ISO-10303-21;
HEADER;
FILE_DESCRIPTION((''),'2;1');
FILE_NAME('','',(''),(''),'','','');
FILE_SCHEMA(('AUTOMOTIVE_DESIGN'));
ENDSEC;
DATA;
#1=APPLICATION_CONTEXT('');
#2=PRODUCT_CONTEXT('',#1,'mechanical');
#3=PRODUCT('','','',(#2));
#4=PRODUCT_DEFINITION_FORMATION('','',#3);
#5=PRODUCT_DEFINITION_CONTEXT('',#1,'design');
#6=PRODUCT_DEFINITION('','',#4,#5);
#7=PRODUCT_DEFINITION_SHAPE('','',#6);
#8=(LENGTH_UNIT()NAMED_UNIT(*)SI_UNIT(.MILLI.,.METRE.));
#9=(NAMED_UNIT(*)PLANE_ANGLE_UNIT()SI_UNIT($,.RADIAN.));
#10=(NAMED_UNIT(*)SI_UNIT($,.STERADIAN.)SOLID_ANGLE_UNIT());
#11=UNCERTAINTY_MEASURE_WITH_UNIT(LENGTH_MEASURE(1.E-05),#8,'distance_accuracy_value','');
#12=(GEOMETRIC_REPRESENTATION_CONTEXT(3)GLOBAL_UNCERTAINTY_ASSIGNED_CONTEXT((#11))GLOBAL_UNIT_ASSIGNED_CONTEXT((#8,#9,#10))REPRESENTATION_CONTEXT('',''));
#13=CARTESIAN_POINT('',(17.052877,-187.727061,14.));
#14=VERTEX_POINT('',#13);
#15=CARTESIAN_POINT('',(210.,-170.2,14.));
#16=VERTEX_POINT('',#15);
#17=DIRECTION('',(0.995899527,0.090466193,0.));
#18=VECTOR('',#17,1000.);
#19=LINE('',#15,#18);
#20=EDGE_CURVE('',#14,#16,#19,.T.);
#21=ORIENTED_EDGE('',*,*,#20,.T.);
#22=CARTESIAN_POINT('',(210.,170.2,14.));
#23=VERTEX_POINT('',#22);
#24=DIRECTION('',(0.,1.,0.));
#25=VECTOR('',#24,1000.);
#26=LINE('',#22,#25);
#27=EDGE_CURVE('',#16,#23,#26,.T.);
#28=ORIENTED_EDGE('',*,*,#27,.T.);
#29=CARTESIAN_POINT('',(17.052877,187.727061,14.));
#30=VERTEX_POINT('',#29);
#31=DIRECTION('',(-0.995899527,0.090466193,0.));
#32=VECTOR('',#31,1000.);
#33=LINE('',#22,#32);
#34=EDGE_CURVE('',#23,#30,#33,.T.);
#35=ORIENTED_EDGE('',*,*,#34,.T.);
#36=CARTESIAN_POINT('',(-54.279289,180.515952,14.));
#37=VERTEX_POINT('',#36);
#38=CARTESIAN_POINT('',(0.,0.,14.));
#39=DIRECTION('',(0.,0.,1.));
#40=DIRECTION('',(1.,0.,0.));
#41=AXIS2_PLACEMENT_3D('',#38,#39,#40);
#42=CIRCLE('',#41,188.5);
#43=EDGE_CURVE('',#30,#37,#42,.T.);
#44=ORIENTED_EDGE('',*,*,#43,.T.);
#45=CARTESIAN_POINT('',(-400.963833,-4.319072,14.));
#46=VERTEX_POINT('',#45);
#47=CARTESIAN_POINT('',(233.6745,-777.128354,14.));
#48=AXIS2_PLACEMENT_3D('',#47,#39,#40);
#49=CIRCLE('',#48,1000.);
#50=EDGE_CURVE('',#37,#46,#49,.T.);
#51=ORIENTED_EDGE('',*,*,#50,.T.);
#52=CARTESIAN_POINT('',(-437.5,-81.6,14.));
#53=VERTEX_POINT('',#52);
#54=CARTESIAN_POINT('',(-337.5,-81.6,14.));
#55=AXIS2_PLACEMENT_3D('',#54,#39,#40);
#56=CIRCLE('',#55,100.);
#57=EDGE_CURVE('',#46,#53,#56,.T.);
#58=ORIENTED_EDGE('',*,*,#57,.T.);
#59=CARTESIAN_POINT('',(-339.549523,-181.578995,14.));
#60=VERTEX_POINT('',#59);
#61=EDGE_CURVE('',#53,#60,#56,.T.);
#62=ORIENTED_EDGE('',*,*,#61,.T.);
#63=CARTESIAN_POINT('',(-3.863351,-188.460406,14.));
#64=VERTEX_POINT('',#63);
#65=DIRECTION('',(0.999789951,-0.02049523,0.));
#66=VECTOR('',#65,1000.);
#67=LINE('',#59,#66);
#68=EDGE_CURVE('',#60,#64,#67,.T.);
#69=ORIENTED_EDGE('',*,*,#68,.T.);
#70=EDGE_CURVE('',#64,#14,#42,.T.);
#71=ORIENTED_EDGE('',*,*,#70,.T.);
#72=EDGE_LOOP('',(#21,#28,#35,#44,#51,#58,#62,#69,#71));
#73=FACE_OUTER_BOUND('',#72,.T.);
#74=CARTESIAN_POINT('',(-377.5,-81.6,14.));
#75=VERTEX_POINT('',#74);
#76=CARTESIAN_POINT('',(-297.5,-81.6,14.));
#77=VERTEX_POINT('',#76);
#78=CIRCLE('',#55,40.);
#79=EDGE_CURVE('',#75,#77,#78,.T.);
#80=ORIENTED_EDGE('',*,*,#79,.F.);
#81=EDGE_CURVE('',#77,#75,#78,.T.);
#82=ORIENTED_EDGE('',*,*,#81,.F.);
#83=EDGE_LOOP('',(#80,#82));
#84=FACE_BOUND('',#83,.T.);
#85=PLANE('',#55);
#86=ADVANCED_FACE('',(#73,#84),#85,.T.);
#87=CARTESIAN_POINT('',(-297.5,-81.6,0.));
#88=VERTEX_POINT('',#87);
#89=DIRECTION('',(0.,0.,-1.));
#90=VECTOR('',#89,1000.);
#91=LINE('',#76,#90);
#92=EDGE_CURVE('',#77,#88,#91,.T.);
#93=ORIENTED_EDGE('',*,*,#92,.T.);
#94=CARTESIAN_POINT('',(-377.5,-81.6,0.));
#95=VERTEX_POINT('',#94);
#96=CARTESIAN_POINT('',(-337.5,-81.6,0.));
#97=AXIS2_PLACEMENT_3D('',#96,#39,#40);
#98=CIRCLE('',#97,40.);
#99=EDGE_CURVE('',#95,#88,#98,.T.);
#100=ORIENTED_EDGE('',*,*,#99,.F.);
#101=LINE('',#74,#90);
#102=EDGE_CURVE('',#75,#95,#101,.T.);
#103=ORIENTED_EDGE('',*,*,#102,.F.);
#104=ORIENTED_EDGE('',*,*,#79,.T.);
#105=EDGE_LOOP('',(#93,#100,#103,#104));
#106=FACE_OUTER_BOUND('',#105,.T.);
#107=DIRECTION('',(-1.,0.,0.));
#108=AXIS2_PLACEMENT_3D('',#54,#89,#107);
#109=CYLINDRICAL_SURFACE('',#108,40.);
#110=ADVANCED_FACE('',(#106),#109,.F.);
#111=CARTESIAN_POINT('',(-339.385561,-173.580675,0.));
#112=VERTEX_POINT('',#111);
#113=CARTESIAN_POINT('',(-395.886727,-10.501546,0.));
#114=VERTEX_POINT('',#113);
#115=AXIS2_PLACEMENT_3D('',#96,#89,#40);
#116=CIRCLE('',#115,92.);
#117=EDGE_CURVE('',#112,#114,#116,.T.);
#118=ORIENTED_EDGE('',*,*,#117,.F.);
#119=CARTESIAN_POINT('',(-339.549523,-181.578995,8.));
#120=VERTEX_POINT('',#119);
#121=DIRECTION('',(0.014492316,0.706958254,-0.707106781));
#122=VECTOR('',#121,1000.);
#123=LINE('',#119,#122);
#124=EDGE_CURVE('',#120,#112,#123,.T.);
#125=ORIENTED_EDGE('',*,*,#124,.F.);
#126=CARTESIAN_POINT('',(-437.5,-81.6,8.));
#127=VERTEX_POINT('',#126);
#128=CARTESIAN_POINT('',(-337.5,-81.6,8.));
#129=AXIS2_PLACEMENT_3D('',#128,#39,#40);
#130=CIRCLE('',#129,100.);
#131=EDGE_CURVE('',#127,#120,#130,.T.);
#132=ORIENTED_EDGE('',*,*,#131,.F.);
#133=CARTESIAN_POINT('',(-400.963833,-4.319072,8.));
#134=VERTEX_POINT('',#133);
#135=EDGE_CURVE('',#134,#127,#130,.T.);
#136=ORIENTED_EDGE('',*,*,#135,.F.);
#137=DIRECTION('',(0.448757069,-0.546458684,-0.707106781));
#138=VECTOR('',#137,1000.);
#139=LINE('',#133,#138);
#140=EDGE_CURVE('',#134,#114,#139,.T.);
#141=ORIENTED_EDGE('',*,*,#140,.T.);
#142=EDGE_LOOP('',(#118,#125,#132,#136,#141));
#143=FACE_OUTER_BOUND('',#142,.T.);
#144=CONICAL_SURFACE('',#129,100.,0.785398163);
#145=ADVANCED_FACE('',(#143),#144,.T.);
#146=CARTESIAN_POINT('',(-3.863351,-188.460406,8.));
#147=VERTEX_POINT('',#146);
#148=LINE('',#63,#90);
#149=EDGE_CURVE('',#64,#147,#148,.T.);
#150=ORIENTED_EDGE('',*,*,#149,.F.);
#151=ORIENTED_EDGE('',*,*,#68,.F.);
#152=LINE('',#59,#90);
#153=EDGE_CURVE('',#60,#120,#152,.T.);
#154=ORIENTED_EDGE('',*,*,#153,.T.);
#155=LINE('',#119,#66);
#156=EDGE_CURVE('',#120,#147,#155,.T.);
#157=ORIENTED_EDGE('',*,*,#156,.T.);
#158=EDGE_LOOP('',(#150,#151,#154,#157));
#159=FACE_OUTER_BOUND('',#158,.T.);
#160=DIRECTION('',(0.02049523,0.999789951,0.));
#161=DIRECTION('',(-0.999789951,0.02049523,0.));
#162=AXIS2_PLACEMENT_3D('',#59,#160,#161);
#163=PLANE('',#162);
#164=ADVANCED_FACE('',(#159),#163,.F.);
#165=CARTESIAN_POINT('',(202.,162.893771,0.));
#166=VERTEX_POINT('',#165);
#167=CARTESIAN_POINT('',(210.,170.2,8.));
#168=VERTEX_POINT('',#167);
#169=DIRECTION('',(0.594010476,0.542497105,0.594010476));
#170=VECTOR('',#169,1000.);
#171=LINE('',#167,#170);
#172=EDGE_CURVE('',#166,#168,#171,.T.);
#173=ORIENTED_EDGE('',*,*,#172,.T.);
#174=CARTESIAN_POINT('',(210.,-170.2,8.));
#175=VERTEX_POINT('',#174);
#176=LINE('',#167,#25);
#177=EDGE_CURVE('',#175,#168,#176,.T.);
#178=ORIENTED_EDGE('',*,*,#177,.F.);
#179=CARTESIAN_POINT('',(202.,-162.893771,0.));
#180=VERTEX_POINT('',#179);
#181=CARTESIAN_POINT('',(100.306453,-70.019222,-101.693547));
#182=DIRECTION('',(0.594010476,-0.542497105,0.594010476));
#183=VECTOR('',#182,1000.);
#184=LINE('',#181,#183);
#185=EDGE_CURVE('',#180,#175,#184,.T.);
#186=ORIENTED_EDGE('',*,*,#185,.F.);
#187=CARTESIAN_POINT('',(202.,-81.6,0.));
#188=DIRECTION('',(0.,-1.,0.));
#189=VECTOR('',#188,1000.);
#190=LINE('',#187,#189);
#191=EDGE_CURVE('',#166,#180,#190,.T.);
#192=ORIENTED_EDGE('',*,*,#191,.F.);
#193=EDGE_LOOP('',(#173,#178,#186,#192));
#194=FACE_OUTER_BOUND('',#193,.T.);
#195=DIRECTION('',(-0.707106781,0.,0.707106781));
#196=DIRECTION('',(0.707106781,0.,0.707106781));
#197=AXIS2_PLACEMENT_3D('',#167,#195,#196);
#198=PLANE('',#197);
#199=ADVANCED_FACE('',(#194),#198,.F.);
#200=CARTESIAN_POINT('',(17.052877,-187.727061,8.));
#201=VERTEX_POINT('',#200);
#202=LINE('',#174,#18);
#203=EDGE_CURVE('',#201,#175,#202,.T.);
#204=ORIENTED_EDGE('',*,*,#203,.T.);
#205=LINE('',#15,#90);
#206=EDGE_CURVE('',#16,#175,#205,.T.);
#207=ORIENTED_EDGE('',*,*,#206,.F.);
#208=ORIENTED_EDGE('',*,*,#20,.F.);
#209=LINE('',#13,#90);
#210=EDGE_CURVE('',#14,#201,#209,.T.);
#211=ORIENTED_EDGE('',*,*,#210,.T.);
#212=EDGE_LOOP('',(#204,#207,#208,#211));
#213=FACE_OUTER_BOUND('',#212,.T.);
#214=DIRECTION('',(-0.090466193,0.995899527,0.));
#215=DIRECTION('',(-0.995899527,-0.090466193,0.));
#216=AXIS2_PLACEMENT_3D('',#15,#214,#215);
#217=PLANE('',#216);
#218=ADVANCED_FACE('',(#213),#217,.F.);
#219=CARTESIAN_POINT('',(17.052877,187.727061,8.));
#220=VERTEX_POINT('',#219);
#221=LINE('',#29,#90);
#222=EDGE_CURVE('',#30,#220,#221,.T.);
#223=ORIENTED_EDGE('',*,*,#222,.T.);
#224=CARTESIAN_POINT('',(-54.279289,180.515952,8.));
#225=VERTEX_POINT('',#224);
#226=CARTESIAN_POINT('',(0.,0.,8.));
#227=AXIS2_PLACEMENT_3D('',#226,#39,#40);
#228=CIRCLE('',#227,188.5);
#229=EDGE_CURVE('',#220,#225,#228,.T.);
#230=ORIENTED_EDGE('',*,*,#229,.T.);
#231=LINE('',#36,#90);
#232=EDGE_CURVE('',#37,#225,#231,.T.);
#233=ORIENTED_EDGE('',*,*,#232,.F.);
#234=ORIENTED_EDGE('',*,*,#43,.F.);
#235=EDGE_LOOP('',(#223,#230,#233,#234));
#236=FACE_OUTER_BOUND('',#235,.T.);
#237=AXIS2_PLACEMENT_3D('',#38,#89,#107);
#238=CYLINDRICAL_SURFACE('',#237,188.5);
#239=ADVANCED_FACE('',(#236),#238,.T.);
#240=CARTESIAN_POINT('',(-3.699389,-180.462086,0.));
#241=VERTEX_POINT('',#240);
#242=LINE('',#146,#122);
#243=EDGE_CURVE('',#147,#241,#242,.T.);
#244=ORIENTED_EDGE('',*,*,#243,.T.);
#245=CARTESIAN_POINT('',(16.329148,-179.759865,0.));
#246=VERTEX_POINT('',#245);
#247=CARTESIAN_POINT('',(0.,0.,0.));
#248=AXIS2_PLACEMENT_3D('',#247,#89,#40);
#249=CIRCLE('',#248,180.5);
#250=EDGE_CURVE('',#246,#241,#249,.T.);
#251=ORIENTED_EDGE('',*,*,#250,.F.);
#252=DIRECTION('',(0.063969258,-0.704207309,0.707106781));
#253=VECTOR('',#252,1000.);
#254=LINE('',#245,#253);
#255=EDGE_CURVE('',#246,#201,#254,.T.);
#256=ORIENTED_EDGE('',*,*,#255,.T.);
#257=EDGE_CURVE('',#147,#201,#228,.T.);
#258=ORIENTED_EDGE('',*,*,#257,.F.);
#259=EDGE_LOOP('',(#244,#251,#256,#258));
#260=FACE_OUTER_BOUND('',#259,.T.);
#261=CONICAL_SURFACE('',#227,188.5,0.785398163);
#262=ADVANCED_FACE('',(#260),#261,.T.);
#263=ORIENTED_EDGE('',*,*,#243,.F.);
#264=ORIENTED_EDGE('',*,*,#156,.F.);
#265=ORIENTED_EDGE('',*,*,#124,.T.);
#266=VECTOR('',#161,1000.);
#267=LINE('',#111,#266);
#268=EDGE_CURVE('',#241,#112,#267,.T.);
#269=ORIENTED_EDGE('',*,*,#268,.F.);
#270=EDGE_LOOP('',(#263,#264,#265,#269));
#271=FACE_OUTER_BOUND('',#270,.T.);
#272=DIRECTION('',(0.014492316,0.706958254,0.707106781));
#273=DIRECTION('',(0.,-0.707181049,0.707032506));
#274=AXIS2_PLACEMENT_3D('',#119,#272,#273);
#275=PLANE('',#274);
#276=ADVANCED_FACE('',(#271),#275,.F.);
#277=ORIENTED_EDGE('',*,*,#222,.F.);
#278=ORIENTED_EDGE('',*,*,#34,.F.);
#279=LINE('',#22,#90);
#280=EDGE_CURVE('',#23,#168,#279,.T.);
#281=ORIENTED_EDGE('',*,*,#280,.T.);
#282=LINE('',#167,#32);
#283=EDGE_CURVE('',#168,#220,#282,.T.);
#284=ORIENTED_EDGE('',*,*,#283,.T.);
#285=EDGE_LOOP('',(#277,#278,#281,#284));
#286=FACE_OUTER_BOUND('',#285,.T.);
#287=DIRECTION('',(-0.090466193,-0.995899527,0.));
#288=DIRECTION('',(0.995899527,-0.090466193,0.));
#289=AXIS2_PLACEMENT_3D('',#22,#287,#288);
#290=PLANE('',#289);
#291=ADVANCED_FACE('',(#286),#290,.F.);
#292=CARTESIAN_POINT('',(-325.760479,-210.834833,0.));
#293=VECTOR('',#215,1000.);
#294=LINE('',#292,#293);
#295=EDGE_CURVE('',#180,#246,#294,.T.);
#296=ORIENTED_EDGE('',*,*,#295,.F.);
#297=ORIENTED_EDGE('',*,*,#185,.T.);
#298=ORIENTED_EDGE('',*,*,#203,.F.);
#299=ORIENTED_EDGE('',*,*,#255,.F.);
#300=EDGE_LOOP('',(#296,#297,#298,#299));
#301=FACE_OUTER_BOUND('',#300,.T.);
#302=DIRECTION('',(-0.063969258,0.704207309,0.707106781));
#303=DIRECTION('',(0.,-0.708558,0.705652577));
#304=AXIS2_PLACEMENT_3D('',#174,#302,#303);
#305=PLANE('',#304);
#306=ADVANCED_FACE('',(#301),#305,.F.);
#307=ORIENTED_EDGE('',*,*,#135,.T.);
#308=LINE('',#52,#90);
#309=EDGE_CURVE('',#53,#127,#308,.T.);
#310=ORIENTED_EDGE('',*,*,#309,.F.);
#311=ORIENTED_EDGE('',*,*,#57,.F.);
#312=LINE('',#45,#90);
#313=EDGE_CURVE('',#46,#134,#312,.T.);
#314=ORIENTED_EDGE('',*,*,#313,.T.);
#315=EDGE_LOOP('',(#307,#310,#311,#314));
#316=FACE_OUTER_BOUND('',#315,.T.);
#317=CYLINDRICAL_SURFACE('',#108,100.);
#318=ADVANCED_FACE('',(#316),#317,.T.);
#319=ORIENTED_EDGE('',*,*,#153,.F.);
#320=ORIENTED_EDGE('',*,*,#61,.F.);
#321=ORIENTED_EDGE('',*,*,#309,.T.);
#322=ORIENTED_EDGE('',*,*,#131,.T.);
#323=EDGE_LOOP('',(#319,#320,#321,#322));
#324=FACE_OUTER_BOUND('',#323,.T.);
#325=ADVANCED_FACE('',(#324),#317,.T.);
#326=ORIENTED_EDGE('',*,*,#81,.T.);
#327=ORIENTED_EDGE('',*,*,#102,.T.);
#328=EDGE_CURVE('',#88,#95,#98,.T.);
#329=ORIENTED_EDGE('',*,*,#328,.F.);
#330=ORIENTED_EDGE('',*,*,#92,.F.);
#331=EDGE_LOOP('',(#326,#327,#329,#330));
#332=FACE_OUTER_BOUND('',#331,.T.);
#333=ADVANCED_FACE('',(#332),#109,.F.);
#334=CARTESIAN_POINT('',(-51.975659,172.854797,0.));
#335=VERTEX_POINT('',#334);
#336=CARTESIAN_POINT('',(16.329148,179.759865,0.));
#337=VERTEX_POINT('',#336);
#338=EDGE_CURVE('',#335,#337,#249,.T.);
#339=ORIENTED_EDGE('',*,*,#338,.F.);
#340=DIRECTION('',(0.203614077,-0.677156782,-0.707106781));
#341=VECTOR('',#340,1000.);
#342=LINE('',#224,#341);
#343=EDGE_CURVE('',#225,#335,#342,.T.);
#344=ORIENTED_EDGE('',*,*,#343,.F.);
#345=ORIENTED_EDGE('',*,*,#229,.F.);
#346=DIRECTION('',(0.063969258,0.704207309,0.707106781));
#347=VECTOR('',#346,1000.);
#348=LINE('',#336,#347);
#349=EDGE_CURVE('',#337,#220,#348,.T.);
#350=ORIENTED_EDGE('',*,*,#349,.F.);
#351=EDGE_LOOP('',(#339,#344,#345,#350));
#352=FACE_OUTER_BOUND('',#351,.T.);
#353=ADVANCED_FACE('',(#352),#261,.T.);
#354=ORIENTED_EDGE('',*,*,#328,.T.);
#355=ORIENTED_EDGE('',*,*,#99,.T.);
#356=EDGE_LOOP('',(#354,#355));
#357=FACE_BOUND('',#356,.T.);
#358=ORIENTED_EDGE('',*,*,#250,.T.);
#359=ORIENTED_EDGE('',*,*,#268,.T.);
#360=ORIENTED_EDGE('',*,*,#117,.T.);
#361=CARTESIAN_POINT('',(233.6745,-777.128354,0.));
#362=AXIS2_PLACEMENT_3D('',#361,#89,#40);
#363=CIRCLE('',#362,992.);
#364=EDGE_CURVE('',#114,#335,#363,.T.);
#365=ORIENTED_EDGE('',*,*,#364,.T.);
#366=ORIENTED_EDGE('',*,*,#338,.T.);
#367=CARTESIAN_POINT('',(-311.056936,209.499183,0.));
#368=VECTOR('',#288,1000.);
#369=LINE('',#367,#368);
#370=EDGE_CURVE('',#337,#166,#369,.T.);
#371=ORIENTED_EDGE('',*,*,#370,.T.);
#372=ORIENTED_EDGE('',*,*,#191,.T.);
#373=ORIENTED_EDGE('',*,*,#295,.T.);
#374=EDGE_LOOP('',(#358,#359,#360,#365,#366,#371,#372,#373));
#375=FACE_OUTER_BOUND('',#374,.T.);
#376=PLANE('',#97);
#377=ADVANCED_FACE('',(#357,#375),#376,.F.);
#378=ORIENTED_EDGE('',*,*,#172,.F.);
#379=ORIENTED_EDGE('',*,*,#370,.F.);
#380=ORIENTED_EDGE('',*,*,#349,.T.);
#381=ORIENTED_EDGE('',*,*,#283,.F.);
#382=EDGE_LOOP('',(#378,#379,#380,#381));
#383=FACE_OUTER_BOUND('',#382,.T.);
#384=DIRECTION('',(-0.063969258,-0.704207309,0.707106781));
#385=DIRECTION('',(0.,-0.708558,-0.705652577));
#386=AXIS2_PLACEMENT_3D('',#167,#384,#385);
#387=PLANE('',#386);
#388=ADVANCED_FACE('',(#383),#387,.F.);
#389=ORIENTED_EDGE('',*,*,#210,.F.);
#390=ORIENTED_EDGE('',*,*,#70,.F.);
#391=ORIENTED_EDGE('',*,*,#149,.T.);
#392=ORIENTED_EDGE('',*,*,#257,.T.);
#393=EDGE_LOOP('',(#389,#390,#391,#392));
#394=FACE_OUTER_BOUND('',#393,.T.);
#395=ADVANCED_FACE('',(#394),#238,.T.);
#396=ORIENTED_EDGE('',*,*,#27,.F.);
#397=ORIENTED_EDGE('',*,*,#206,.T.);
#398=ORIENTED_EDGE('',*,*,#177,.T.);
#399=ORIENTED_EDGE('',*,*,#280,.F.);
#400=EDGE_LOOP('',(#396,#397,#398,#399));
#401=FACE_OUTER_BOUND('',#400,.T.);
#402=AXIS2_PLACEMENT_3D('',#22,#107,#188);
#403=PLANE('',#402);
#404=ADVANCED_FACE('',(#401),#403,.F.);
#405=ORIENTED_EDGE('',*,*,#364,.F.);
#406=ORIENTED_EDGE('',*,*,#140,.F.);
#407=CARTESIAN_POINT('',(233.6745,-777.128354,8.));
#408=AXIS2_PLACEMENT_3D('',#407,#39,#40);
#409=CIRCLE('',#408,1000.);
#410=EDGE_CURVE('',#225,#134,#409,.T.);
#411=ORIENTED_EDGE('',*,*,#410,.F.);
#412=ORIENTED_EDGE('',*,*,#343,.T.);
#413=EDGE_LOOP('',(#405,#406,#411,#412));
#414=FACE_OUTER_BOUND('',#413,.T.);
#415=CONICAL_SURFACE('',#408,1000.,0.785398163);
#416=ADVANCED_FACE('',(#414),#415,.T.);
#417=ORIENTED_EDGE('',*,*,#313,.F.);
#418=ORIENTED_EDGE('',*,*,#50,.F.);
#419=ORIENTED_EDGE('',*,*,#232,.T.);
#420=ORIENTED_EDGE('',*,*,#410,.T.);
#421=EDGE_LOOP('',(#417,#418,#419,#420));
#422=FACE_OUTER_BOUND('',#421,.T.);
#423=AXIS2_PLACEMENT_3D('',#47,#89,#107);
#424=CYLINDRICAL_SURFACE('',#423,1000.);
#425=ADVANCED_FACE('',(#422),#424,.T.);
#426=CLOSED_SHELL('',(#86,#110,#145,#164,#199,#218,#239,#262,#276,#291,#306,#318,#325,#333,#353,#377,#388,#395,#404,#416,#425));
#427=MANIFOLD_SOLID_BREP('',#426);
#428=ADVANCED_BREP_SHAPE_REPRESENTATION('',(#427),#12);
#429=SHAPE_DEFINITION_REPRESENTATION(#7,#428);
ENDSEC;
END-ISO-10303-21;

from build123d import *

# Parameters (mm, degrees)
SKETCH1_R           = 40
BOSS_EXTRUDE1_DEPTH = 14
CHAMFER1_SIZE       = 8


with BuildPart() as part:
    # Sketch1 → Boss-Extrude1 (new body)
    with BuildSketch(Plane.XY):
        with BuildLine():
            Line((210, 170.2), (17.052877352, 187.727060846))
            ThreePointArc((17.052877352, 187.727060846), (-18.959205139, 187.54412425), (-54.27928922, 180.515951544))
            ThreePointArc((-54.27928922, 180.515951544), (-236.788094268, 105.291584642), (-400.963833305, -4.319071808))
            ThreePointArc((-400.963833305, -4.319071808), (-431.989523554, -114.33728667), (-339.549522969, -181.578995072))
            Line((-339.549522969, -181.578995072), (-3.863350797, -188.460405711))
            ThreePointArc((-3.863350797, -188.460405711), (6.604949005, -188.384247347), (17.052877352, -187.727060846))
            Line((17.052877352, -187.727060846), (210, -170.2))
            Line((210, -170.2), (210, 170.2))
        make_face()
        with Locations((-337.5, -81.6)):
            Circle(SKETCH1_R, mode=Mode.SUBTRACT)
    extrude(amount=BOSS_EXTRUDE1_DEPTH)

    # Chamfer1
    chamfer1_edges = [part.edges().sort_by_distance(p)[0] for p in [
        (-171.706436883, -185.019700391, 0),
        (-431.989523554, -114.33728667, 0),
        (-236.788094268, 105.291584642, 0),
        (-18.959205139, 187.54412425, 0),
        (113.526438676, 178.963530423, 0),
        (210, 0, 0),
        (113.526438676, -178.963530423, 0),
        (6.604949005, -188.384247347, 0),
    ]]
    chamfer(chamfer1_edges, length=CHAMFER1_SIZE)


solid = part.part
